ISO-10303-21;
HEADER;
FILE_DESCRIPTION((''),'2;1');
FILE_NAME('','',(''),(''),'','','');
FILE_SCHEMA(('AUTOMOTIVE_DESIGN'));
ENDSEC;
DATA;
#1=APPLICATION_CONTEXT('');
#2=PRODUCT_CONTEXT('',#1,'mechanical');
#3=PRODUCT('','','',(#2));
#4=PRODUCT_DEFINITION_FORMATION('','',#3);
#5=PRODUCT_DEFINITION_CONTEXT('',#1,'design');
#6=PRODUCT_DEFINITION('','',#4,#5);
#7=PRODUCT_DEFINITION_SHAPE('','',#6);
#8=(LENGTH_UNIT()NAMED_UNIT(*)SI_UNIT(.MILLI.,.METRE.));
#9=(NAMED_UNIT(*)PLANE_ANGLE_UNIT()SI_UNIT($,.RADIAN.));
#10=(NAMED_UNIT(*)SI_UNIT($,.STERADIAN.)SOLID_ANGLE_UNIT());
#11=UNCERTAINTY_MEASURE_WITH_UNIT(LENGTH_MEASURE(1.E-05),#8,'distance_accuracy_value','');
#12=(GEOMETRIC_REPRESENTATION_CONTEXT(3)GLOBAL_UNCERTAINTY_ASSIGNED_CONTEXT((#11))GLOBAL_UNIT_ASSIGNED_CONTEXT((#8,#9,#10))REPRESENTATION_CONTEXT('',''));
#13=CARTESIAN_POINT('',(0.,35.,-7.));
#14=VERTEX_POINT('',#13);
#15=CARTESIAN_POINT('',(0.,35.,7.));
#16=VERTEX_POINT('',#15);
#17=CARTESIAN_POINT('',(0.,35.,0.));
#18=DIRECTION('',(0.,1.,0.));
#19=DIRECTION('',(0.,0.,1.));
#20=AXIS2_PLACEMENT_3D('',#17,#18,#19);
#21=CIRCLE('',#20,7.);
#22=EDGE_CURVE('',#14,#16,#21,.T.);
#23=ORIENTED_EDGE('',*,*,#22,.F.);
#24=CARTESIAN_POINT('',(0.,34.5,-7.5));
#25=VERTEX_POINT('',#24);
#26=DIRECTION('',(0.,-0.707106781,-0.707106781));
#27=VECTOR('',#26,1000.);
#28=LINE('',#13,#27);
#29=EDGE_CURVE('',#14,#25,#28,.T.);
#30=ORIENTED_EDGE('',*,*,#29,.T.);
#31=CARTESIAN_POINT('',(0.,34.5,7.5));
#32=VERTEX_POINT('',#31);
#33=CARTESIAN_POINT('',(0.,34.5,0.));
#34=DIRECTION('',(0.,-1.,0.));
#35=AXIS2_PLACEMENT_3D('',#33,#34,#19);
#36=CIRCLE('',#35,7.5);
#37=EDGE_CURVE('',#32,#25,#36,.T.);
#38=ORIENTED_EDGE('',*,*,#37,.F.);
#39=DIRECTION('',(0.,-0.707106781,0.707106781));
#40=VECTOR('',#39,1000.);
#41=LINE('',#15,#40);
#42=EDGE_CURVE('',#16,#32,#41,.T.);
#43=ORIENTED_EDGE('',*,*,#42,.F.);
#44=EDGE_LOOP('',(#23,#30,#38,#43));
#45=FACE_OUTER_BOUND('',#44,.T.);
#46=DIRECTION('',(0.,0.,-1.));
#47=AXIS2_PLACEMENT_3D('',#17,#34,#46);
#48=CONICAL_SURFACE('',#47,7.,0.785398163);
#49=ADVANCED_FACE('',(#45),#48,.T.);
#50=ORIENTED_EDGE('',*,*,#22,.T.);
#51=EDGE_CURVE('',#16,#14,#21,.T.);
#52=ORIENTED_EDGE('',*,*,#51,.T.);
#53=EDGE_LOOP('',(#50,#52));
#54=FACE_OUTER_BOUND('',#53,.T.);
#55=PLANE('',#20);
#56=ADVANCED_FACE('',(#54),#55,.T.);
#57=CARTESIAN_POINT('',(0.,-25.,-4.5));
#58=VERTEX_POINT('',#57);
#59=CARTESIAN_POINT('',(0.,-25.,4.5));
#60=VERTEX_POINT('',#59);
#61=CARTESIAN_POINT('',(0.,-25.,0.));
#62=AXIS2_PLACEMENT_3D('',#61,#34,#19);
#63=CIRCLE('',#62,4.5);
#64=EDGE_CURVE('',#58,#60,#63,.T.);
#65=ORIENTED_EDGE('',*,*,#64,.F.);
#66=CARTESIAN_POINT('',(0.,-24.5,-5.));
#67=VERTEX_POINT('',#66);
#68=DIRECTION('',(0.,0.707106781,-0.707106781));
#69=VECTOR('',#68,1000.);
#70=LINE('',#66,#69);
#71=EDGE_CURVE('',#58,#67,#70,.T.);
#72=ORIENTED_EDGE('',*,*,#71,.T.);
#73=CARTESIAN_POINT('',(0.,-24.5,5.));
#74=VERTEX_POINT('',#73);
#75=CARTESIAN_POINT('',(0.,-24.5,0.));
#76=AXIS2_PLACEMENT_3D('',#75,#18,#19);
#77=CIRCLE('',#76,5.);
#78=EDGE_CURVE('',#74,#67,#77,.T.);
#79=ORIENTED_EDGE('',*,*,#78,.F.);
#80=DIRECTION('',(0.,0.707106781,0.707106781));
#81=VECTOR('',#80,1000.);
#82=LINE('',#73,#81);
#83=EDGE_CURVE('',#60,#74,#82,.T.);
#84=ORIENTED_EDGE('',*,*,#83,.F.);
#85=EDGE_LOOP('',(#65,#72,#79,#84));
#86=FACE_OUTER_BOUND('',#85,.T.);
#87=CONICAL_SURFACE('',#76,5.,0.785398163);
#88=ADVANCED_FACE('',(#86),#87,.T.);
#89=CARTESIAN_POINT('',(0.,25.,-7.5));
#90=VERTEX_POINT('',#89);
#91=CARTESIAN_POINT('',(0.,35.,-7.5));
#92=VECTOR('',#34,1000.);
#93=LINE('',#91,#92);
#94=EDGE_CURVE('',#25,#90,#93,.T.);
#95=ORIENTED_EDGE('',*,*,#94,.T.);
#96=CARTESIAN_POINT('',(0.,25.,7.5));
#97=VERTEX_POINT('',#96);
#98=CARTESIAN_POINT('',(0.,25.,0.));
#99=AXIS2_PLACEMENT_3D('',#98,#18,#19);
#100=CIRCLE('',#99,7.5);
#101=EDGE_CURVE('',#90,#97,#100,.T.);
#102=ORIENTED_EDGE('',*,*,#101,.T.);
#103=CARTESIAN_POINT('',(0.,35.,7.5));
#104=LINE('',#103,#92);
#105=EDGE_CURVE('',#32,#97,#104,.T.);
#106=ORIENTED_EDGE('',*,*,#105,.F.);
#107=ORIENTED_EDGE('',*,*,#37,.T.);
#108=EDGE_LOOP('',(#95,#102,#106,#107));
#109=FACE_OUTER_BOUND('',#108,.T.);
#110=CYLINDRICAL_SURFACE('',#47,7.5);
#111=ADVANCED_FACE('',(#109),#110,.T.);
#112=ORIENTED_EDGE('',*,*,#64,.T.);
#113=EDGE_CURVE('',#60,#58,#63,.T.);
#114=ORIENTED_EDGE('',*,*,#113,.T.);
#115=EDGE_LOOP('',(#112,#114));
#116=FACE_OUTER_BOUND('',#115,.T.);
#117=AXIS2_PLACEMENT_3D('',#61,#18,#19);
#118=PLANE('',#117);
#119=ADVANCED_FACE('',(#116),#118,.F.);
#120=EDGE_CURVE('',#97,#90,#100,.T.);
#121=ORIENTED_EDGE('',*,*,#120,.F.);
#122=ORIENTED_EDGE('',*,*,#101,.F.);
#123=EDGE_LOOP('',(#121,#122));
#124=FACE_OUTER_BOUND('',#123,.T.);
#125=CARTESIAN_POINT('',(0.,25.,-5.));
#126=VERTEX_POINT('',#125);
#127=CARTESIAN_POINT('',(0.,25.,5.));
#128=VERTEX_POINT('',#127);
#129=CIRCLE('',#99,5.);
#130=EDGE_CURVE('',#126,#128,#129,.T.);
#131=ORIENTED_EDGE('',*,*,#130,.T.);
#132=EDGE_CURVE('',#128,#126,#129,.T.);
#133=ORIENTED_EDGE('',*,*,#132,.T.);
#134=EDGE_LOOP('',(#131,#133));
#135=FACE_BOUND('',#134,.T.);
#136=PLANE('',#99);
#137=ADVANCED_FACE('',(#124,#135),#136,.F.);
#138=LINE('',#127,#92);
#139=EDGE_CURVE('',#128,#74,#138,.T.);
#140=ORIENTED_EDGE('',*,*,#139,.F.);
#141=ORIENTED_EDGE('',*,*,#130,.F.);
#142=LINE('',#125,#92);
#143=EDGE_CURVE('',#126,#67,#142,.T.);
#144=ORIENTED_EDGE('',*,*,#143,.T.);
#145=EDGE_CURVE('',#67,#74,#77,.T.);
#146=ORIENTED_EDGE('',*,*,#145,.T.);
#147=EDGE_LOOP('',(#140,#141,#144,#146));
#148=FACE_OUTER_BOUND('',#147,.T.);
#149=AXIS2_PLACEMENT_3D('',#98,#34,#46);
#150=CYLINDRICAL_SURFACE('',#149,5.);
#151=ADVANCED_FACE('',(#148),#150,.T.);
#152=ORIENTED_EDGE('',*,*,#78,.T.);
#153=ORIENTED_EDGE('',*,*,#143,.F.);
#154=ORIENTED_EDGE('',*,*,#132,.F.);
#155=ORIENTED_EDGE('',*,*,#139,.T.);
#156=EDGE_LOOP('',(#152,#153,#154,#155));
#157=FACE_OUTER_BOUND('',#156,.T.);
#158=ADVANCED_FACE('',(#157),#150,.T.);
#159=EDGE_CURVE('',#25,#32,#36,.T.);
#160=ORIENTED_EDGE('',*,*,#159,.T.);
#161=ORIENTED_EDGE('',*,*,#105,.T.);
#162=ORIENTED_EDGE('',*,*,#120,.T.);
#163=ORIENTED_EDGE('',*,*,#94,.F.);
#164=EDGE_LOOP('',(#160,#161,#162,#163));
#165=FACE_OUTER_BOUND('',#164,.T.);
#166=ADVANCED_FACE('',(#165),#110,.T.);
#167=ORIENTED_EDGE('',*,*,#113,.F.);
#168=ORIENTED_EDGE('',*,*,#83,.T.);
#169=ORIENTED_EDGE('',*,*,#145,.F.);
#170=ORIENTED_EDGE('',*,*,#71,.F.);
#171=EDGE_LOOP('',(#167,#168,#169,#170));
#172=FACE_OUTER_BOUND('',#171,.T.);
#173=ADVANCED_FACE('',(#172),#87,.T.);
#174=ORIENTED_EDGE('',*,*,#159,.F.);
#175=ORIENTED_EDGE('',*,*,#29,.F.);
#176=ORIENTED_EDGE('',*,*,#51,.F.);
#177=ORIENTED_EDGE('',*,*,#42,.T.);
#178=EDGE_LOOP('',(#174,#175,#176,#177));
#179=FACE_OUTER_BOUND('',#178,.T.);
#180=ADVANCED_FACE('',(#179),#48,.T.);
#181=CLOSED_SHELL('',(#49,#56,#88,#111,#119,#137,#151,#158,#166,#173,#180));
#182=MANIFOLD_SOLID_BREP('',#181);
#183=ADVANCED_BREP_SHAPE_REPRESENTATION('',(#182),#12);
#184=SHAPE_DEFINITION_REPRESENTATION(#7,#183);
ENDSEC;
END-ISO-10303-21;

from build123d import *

# Parameters (mm, degrees)
SKETCH_1_R      = 5
EXTRUDE_1_DEPTH = 25
SKETCH_2_R      = 7.5
EXTRUDE_2_DEPTH = 10
CHAMFER_1_SIZE  = 0.5


with BuildPart() as part:
    # 草图1 → 凸台-拉伸1 (new, symmetric)
    with BuildSketch(Plane(origin=(0, 0, 0), x_dir=(1, 0, 0), z_dir=(0, 1, 0))):
        with Locations(Location((0, 0, 0), (0, 0, 270))):
            Circle(SKETCH_1_R)
    extrude(amount=EXTRUDE_1_DEPTH, both=True)

    # 草图2 → 凸台-拉伸2 (add)
    with BuildSketch(Plane(origin=(0, 25, 0), x_dir=(1, 0, 0), z_dir=(0, 1, 0))):
        with Locations(Location((0, 0, 0), (0, 0, 270))):
            Circle(SKETCH_2_R)
    extrude(amount=EXTRUDE_2_DEPTH)

    # 倒角1
    chamfer_1_edges = [part.edges().sort_by_distance(p)[0] for p in [
        (0, -25, -5),
        (0, 35, -7.5),
    ]]
    chamfer(chamfer_1_edges, length=CHAMFER_1_SIZE)


solid = part.part
